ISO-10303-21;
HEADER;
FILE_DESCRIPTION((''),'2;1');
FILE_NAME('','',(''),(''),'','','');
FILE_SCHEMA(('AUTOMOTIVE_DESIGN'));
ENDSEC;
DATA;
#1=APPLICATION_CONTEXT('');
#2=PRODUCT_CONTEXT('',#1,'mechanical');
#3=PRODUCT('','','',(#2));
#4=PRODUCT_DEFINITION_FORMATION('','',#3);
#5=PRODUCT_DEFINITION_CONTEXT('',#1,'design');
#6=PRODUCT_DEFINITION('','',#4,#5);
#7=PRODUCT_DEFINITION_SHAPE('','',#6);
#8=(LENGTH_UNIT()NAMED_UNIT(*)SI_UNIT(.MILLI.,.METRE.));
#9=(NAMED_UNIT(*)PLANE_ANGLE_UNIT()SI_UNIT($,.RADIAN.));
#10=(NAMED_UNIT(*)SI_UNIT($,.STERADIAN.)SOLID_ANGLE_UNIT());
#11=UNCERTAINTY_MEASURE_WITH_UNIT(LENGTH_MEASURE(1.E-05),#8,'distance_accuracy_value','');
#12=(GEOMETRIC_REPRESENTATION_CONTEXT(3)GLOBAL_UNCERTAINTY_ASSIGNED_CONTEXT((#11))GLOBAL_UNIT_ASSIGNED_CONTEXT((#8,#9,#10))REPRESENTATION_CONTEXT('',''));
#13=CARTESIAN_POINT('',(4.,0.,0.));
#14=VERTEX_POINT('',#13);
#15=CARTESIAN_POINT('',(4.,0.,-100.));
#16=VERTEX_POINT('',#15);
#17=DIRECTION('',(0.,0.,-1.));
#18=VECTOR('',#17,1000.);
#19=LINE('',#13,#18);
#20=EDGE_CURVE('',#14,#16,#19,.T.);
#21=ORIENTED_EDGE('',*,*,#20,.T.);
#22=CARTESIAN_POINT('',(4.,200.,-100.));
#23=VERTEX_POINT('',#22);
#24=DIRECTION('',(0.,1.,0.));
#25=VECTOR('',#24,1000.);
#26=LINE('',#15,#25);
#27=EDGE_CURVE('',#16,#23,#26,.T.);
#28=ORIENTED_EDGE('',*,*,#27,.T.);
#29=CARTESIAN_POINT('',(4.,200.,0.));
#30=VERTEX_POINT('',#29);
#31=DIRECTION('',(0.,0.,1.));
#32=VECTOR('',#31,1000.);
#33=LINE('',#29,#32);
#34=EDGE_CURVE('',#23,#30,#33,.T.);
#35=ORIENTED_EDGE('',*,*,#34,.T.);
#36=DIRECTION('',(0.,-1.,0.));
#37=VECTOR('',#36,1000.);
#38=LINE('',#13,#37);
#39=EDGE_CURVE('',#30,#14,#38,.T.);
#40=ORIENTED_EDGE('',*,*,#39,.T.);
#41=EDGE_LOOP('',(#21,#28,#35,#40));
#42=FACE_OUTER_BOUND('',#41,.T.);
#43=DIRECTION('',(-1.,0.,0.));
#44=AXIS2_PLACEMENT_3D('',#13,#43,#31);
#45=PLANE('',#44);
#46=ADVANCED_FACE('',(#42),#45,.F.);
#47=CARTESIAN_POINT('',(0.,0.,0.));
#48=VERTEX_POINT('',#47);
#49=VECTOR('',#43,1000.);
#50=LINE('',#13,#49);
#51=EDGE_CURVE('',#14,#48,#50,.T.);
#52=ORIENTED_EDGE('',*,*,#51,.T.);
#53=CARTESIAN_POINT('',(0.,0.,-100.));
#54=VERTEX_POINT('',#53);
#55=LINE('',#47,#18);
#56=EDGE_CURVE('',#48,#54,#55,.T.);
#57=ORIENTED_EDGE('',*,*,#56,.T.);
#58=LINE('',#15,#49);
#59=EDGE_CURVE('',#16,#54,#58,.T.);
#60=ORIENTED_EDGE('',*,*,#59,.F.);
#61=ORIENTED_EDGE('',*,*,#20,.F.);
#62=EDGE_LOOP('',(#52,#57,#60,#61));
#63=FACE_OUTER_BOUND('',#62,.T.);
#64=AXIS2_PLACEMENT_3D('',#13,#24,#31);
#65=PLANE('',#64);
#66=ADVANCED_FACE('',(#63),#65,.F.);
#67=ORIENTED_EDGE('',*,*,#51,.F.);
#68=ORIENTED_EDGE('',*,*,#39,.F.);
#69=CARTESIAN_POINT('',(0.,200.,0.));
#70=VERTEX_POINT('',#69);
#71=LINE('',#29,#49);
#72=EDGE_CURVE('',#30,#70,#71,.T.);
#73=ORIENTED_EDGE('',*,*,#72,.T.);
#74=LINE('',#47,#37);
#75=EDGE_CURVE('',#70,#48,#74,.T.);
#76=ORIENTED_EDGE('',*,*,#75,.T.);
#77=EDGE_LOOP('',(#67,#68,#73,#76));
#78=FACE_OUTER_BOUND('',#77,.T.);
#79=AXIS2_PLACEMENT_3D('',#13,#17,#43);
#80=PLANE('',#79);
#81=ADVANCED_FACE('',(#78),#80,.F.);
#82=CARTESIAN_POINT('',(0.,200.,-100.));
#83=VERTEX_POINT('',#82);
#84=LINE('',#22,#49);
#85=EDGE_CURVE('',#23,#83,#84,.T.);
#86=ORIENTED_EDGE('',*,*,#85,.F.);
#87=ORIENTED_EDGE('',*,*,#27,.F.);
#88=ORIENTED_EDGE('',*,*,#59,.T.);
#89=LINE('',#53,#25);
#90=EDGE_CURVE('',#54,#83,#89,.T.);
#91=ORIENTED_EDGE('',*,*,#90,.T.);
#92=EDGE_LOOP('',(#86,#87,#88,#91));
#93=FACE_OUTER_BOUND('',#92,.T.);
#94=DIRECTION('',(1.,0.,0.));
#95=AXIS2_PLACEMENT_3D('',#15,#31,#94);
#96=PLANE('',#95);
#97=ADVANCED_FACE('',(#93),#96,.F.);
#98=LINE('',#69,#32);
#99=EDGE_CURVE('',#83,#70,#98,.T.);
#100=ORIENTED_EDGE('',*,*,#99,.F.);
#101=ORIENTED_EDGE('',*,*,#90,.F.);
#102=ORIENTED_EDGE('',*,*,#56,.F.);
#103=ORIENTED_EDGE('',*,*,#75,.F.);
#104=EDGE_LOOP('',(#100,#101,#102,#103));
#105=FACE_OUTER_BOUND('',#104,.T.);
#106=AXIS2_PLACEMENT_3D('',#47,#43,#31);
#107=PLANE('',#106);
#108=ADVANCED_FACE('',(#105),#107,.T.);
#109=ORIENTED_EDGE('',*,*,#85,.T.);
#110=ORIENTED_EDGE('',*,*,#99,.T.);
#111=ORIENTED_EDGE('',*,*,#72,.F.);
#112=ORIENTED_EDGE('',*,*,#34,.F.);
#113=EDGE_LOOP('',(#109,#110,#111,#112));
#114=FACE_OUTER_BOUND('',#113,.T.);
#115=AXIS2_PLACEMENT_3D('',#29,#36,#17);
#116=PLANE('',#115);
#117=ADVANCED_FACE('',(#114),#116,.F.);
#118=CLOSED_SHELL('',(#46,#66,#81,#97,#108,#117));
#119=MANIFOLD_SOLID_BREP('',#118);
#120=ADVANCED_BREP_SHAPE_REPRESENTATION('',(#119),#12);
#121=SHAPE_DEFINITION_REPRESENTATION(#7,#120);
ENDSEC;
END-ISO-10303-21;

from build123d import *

# Parameters (mm, degrees)
SKETCH_1_W      = 100
SKETCH_1_H      = 200
EXTRUDE_1_DEPTH = 4


with BuildPart() as part:
    # 草图1 → 凸台-拉伸1 (new body)
    with BuildSketch(Plane(origin=(0, 0, 0), x_dir=(0, 0, -1), z_dir=(1, 0, 0))):
        with Locations((50, 100)):
            Rectangle(SKETCH_1_W, SKETCH_1_H)
    extrude(amount=EXTRUDE_1_DEPTH)


solid = part.part
